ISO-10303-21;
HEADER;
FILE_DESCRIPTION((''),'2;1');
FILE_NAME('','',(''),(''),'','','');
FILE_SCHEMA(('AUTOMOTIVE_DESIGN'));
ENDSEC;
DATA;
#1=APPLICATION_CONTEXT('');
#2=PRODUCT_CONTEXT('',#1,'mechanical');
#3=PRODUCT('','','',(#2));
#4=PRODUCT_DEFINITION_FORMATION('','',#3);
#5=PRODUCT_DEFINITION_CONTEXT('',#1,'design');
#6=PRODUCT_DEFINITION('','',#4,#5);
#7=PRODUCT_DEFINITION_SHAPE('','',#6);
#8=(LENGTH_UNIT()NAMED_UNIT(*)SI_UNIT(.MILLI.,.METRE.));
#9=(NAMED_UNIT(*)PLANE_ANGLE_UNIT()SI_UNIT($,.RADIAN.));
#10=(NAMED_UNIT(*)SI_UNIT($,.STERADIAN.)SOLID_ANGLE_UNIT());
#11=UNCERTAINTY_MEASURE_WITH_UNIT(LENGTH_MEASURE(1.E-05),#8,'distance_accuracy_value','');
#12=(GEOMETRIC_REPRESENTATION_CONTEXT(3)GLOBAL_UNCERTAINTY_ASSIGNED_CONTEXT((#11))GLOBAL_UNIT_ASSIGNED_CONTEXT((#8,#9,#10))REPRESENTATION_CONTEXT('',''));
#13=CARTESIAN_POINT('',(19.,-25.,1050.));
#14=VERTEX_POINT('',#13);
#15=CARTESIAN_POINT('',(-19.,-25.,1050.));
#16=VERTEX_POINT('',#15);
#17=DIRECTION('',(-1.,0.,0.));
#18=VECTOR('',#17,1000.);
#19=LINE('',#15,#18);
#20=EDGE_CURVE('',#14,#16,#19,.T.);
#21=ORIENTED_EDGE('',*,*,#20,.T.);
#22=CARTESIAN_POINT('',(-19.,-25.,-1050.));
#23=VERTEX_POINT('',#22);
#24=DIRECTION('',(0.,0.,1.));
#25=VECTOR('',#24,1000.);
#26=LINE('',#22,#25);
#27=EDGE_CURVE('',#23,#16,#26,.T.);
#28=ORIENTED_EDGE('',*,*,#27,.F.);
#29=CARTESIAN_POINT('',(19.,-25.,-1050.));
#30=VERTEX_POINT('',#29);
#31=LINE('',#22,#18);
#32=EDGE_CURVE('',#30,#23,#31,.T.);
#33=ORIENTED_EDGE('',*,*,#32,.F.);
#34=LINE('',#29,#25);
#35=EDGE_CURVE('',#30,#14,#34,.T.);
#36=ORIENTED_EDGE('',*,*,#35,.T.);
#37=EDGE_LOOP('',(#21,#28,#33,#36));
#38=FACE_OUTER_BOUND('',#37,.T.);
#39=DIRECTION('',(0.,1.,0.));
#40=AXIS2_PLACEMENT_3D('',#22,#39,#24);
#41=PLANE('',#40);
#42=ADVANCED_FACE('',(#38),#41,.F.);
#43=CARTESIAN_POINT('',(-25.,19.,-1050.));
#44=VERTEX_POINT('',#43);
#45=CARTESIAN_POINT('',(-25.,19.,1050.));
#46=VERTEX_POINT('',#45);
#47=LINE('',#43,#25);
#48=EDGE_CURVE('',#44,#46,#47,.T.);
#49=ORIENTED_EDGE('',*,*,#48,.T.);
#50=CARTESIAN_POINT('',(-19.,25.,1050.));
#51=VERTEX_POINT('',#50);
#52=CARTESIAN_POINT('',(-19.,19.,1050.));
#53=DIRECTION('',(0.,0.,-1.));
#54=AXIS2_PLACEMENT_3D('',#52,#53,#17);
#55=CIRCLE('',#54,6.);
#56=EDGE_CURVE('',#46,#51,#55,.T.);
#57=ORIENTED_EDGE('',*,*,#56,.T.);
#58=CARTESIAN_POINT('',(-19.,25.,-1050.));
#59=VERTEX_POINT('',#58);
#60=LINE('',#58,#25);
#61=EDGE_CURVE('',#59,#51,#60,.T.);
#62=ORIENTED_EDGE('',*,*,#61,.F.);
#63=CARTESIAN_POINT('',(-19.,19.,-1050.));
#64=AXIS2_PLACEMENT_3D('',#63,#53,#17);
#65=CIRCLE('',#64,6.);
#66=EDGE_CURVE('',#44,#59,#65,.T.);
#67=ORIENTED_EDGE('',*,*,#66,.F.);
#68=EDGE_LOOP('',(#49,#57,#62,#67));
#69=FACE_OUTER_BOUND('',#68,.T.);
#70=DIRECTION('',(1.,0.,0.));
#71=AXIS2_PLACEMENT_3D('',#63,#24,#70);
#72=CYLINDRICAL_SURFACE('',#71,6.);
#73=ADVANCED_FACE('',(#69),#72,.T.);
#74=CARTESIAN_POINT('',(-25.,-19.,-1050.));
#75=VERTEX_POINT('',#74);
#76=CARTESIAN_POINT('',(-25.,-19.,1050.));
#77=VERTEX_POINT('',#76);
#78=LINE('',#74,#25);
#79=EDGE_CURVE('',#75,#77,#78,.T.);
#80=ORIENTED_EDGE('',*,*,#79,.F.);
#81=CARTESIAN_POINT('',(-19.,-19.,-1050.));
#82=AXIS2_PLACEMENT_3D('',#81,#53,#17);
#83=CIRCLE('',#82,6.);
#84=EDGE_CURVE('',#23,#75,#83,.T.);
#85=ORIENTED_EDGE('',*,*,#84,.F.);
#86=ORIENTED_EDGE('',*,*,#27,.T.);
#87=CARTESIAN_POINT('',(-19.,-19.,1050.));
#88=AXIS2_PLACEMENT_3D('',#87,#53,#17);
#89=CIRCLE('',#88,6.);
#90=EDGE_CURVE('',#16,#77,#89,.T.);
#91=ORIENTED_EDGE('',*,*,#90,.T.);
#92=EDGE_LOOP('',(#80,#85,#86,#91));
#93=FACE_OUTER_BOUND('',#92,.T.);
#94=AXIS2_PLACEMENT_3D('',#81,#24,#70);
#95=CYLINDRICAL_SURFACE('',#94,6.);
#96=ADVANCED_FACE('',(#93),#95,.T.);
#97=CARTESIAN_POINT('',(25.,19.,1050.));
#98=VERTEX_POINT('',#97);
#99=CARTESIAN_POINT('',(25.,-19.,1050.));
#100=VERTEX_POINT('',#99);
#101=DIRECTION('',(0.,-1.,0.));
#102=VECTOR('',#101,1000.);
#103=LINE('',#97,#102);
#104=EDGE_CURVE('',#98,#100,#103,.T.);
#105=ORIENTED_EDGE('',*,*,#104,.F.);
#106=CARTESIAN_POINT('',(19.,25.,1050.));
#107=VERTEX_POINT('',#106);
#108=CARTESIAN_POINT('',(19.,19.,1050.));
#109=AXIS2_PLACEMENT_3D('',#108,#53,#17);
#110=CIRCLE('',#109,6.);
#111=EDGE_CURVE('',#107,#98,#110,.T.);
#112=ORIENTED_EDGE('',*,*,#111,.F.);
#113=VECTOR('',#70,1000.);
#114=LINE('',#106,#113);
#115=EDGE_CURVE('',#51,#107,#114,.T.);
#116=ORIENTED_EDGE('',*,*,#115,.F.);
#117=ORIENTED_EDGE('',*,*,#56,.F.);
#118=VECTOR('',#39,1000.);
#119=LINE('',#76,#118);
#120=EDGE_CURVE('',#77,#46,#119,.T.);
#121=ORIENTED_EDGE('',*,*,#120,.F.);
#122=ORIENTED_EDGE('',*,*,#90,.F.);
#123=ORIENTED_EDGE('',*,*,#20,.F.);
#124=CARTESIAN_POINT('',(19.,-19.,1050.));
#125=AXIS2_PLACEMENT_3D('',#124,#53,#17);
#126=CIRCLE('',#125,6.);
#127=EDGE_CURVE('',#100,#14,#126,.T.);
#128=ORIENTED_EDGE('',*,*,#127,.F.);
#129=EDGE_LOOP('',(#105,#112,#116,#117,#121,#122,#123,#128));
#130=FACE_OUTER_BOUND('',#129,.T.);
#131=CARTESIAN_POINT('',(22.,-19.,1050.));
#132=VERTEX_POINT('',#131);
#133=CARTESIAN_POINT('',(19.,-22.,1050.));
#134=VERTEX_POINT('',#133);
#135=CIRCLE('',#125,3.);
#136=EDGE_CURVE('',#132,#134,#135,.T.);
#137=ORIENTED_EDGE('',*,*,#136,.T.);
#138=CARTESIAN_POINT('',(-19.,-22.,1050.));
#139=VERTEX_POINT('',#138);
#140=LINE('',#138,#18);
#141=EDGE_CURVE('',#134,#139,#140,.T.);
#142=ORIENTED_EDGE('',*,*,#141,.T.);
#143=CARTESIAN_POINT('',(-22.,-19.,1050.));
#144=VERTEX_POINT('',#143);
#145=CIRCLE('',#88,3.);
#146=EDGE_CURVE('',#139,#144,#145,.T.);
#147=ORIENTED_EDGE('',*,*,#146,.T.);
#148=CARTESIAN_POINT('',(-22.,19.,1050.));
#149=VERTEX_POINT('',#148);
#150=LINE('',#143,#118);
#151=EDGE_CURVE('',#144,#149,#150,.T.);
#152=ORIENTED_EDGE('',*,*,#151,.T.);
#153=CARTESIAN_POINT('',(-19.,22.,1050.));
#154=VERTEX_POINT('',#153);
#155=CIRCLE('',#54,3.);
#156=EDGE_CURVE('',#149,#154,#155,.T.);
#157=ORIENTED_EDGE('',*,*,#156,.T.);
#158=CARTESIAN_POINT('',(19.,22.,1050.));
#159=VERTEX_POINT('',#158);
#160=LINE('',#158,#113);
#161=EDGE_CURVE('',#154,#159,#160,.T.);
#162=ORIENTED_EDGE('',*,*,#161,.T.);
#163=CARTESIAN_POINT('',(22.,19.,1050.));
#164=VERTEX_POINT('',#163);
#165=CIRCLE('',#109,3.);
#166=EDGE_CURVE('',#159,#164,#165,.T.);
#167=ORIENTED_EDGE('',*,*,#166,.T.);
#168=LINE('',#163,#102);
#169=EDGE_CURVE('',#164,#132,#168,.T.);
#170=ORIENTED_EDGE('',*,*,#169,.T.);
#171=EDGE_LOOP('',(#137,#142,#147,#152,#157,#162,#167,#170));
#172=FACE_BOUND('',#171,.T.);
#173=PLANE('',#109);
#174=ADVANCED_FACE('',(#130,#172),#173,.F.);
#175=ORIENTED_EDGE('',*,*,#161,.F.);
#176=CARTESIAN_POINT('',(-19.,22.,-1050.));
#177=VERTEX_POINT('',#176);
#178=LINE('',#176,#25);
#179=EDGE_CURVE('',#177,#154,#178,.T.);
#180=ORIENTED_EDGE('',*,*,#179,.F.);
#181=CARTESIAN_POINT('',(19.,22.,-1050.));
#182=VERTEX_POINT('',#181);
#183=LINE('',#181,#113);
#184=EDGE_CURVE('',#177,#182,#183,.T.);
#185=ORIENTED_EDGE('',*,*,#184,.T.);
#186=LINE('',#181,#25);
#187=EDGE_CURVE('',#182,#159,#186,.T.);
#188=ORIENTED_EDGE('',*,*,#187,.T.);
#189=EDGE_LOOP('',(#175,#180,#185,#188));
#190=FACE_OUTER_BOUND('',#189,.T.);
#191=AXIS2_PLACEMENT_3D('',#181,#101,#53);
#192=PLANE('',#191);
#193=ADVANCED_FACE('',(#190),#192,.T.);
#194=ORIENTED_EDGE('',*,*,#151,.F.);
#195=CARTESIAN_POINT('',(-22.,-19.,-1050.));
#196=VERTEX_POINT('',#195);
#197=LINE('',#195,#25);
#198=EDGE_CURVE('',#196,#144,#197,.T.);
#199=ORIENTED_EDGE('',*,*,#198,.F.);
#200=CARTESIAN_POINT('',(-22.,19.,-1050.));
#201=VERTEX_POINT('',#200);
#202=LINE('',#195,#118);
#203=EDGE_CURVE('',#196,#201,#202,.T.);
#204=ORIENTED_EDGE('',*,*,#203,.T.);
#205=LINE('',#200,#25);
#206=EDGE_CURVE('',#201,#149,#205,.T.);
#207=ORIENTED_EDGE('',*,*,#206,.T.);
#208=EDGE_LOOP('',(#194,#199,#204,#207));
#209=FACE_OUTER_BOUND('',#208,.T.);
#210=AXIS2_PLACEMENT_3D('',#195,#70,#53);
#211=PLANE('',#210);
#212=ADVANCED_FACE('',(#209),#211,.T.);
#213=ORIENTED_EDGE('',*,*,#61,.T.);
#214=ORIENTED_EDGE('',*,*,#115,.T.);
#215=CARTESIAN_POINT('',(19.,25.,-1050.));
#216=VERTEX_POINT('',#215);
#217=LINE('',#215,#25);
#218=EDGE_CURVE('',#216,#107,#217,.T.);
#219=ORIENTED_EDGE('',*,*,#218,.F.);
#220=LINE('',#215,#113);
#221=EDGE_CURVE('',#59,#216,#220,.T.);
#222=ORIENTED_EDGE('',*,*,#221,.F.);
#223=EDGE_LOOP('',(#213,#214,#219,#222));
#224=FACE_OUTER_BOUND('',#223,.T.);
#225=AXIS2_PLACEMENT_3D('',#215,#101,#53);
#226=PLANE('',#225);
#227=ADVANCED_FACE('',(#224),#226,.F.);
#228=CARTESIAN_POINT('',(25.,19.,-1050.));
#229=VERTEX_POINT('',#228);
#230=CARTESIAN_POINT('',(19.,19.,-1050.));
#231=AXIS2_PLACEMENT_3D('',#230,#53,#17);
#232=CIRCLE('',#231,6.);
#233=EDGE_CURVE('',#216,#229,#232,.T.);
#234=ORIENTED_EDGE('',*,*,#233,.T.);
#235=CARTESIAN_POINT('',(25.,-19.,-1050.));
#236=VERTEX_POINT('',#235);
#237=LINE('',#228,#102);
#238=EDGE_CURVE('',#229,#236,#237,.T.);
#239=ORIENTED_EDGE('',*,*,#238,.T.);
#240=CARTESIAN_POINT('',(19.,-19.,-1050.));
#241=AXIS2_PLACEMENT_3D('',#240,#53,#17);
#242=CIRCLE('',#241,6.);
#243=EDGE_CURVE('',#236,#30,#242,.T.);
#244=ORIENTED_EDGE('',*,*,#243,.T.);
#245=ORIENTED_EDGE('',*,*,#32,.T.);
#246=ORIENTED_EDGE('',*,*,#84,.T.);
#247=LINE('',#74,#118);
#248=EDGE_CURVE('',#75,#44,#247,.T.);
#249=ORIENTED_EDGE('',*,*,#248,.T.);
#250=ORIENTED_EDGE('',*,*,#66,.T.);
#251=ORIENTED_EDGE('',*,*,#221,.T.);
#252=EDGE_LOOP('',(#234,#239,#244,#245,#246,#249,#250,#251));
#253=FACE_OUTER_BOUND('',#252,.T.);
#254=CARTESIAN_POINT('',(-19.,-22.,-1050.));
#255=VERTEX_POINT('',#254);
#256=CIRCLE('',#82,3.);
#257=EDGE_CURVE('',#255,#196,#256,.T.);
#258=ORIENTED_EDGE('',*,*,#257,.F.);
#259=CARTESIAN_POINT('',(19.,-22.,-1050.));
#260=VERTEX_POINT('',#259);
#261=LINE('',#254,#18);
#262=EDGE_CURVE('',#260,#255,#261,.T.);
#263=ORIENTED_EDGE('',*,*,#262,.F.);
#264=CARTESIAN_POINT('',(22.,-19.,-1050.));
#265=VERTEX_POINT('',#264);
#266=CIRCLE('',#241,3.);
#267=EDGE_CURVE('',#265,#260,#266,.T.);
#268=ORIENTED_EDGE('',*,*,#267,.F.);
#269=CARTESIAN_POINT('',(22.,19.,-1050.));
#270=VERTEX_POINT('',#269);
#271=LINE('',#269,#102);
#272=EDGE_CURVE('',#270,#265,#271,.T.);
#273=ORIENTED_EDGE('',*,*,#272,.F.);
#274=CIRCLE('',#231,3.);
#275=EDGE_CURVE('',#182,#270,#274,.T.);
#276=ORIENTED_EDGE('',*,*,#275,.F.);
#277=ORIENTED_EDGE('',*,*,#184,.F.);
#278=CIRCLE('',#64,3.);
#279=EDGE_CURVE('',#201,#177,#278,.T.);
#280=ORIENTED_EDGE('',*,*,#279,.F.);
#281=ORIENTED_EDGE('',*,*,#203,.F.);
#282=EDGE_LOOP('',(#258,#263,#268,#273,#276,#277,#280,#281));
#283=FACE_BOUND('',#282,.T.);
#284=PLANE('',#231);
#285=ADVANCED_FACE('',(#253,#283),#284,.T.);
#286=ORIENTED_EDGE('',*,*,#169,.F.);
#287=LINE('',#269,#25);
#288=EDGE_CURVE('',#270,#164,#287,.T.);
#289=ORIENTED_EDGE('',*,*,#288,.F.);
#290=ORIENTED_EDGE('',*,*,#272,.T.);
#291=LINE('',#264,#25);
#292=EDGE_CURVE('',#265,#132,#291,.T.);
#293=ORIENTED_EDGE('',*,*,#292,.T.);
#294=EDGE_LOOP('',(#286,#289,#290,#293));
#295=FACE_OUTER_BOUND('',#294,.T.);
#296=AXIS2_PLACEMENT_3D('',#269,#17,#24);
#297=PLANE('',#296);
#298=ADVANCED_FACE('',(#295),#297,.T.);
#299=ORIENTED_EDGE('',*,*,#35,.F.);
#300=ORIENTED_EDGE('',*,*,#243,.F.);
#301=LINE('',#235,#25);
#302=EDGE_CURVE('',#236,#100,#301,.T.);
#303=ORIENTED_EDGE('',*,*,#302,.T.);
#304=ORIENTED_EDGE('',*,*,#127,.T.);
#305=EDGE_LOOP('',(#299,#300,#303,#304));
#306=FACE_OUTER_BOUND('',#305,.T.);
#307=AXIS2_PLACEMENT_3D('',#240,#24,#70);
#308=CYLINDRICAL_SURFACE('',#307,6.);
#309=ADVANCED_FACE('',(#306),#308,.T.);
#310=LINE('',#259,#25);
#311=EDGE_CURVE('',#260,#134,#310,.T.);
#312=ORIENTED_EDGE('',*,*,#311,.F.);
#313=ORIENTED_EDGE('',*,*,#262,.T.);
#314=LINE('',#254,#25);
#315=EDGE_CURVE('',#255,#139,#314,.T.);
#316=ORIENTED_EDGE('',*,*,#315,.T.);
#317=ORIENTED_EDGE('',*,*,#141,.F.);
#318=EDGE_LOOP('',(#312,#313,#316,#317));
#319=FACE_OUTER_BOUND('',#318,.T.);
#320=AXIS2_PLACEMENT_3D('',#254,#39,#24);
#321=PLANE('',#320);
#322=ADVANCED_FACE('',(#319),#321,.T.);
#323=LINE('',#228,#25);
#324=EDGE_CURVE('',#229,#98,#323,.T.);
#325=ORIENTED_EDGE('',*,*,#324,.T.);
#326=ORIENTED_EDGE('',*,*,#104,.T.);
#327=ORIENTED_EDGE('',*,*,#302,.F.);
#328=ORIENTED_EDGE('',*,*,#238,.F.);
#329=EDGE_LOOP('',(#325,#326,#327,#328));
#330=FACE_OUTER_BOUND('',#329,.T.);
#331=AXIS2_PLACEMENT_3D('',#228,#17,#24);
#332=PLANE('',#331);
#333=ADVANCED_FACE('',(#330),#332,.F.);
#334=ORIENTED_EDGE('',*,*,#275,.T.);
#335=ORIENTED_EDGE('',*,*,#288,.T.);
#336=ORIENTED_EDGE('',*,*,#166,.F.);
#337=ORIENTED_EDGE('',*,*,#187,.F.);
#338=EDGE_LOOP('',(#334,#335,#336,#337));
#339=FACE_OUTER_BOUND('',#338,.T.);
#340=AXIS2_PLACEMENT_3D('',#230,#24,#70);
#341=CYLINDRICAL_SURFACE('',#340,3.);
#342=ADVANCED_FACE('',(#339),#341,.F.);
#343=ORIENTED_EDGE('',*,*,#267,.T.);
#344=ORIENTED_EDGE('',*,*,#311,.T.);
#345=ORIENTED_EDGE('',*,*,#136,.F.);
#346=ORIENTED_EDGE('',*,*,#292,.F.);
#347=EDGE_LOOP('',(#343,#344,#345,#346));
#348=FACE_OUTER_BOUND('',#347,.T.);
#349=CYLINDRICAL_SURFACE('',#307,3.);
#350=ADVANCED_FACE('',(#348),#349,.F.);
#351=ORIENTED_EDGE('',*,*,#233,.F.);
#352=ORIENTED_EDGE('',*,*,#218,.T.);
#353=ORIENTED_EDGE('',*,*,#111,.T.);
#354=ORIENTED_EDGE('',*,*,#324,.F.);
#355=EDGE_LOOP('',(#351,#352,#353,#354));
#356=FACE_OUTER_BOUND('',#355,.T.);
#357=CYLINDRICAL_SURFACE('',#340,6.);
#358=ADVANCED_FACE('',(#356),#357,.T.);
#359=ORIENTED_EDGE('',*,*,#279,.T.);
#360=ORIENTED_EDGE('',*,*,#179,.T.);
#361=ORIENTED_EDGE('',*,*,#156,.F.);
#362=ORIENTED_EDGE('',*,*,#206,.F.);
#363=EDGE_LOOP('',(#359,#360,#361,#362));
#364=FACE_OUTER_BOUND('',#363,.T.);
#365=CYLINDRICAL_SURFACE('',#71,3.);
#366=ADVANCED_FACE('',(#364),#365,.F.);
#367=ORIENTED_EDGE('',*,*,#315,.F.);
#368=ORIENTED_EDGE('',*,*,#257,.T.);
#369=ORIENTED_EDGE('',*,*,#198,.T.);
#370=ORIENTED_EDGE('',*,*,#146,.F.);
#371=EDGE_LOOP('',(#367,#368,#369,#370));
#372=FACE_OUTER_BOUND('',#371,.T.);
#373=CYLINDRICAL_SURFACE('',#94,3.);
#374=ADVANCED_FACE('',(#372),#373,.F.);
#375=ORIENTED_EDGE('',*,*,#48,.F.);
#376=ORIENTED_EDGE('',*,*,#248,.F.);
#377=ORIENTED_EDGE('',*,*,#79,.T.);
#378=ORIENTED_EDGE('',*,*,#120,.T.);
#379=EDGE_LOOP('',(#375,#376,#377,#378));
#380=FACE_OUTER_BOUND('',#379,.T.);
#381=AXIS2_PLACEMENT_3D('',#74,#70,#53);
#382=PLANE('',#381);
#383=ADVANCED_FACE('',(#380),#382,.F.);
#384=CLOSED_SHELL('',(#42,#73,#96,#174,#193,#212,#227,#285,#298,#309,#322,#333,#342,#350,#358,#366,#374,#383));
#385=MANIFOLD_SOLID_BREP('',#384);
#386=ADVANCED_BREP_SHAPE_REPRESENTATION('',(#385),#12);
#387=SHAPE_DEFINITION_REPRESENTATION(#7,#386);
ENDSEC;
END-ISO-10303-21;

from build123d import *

# Parameters (mm, degrees)
GB_6728_1986_050_X_50_X_3_1_DEPTH = 2100


with BuildPart() as part:
    # Sketch1 → Gb／6728-1986方形空心型钢 050 X 50 X 3(1) (new body)
    with BuildSketch(Plane.YX.offset(-1050)):
        with BuildLine():
            Line((-19, -25), (19, -25))
            ThreePointArc((19, -25), (23.242640687, -23.242640687), (25, -19))
            Line((25, -19), (25, 19))
            ThreePointArc((25, 19), (23.242640687, 23.242640687), (19, 25))
            Line((19, 25), (-19, 25))
            ThreePointArc((-19, 25), (-23.242640687, 23.242640687), (-25, 19))
            Line((-25, 19), (-25, -19))
            ThreePointArc((-25, -19), (-23.242640687, -23.242640687), (-19, -25))
        make_face()
        with BuildLine():
            Line((-19, -22), (19, -22))
            ThreePointArc((19, -22), (21.121320344, -21.121320344), (22, -19))
            Line((22, -19), (22, 19))
            ThreePointArc((22, 19), (21.121320344, 21.121320344), (19, 22))
            Line((19, 22), (-19, 22))
            ThreePointArc((-19, 22), (-21.121320344, 21.121320344), (-22, 19))
            Line((-22, 19), (-22, -19))
            ThreePointArc((-22, -19), (-21.121320344, -21.121320344), (-19, -22))
        make_face(mode=Mode.SUBTRACT)
    extrude(amount=GB_6728_1986_050_X_50_X_3_1_DEPTH)


solid = part.part
